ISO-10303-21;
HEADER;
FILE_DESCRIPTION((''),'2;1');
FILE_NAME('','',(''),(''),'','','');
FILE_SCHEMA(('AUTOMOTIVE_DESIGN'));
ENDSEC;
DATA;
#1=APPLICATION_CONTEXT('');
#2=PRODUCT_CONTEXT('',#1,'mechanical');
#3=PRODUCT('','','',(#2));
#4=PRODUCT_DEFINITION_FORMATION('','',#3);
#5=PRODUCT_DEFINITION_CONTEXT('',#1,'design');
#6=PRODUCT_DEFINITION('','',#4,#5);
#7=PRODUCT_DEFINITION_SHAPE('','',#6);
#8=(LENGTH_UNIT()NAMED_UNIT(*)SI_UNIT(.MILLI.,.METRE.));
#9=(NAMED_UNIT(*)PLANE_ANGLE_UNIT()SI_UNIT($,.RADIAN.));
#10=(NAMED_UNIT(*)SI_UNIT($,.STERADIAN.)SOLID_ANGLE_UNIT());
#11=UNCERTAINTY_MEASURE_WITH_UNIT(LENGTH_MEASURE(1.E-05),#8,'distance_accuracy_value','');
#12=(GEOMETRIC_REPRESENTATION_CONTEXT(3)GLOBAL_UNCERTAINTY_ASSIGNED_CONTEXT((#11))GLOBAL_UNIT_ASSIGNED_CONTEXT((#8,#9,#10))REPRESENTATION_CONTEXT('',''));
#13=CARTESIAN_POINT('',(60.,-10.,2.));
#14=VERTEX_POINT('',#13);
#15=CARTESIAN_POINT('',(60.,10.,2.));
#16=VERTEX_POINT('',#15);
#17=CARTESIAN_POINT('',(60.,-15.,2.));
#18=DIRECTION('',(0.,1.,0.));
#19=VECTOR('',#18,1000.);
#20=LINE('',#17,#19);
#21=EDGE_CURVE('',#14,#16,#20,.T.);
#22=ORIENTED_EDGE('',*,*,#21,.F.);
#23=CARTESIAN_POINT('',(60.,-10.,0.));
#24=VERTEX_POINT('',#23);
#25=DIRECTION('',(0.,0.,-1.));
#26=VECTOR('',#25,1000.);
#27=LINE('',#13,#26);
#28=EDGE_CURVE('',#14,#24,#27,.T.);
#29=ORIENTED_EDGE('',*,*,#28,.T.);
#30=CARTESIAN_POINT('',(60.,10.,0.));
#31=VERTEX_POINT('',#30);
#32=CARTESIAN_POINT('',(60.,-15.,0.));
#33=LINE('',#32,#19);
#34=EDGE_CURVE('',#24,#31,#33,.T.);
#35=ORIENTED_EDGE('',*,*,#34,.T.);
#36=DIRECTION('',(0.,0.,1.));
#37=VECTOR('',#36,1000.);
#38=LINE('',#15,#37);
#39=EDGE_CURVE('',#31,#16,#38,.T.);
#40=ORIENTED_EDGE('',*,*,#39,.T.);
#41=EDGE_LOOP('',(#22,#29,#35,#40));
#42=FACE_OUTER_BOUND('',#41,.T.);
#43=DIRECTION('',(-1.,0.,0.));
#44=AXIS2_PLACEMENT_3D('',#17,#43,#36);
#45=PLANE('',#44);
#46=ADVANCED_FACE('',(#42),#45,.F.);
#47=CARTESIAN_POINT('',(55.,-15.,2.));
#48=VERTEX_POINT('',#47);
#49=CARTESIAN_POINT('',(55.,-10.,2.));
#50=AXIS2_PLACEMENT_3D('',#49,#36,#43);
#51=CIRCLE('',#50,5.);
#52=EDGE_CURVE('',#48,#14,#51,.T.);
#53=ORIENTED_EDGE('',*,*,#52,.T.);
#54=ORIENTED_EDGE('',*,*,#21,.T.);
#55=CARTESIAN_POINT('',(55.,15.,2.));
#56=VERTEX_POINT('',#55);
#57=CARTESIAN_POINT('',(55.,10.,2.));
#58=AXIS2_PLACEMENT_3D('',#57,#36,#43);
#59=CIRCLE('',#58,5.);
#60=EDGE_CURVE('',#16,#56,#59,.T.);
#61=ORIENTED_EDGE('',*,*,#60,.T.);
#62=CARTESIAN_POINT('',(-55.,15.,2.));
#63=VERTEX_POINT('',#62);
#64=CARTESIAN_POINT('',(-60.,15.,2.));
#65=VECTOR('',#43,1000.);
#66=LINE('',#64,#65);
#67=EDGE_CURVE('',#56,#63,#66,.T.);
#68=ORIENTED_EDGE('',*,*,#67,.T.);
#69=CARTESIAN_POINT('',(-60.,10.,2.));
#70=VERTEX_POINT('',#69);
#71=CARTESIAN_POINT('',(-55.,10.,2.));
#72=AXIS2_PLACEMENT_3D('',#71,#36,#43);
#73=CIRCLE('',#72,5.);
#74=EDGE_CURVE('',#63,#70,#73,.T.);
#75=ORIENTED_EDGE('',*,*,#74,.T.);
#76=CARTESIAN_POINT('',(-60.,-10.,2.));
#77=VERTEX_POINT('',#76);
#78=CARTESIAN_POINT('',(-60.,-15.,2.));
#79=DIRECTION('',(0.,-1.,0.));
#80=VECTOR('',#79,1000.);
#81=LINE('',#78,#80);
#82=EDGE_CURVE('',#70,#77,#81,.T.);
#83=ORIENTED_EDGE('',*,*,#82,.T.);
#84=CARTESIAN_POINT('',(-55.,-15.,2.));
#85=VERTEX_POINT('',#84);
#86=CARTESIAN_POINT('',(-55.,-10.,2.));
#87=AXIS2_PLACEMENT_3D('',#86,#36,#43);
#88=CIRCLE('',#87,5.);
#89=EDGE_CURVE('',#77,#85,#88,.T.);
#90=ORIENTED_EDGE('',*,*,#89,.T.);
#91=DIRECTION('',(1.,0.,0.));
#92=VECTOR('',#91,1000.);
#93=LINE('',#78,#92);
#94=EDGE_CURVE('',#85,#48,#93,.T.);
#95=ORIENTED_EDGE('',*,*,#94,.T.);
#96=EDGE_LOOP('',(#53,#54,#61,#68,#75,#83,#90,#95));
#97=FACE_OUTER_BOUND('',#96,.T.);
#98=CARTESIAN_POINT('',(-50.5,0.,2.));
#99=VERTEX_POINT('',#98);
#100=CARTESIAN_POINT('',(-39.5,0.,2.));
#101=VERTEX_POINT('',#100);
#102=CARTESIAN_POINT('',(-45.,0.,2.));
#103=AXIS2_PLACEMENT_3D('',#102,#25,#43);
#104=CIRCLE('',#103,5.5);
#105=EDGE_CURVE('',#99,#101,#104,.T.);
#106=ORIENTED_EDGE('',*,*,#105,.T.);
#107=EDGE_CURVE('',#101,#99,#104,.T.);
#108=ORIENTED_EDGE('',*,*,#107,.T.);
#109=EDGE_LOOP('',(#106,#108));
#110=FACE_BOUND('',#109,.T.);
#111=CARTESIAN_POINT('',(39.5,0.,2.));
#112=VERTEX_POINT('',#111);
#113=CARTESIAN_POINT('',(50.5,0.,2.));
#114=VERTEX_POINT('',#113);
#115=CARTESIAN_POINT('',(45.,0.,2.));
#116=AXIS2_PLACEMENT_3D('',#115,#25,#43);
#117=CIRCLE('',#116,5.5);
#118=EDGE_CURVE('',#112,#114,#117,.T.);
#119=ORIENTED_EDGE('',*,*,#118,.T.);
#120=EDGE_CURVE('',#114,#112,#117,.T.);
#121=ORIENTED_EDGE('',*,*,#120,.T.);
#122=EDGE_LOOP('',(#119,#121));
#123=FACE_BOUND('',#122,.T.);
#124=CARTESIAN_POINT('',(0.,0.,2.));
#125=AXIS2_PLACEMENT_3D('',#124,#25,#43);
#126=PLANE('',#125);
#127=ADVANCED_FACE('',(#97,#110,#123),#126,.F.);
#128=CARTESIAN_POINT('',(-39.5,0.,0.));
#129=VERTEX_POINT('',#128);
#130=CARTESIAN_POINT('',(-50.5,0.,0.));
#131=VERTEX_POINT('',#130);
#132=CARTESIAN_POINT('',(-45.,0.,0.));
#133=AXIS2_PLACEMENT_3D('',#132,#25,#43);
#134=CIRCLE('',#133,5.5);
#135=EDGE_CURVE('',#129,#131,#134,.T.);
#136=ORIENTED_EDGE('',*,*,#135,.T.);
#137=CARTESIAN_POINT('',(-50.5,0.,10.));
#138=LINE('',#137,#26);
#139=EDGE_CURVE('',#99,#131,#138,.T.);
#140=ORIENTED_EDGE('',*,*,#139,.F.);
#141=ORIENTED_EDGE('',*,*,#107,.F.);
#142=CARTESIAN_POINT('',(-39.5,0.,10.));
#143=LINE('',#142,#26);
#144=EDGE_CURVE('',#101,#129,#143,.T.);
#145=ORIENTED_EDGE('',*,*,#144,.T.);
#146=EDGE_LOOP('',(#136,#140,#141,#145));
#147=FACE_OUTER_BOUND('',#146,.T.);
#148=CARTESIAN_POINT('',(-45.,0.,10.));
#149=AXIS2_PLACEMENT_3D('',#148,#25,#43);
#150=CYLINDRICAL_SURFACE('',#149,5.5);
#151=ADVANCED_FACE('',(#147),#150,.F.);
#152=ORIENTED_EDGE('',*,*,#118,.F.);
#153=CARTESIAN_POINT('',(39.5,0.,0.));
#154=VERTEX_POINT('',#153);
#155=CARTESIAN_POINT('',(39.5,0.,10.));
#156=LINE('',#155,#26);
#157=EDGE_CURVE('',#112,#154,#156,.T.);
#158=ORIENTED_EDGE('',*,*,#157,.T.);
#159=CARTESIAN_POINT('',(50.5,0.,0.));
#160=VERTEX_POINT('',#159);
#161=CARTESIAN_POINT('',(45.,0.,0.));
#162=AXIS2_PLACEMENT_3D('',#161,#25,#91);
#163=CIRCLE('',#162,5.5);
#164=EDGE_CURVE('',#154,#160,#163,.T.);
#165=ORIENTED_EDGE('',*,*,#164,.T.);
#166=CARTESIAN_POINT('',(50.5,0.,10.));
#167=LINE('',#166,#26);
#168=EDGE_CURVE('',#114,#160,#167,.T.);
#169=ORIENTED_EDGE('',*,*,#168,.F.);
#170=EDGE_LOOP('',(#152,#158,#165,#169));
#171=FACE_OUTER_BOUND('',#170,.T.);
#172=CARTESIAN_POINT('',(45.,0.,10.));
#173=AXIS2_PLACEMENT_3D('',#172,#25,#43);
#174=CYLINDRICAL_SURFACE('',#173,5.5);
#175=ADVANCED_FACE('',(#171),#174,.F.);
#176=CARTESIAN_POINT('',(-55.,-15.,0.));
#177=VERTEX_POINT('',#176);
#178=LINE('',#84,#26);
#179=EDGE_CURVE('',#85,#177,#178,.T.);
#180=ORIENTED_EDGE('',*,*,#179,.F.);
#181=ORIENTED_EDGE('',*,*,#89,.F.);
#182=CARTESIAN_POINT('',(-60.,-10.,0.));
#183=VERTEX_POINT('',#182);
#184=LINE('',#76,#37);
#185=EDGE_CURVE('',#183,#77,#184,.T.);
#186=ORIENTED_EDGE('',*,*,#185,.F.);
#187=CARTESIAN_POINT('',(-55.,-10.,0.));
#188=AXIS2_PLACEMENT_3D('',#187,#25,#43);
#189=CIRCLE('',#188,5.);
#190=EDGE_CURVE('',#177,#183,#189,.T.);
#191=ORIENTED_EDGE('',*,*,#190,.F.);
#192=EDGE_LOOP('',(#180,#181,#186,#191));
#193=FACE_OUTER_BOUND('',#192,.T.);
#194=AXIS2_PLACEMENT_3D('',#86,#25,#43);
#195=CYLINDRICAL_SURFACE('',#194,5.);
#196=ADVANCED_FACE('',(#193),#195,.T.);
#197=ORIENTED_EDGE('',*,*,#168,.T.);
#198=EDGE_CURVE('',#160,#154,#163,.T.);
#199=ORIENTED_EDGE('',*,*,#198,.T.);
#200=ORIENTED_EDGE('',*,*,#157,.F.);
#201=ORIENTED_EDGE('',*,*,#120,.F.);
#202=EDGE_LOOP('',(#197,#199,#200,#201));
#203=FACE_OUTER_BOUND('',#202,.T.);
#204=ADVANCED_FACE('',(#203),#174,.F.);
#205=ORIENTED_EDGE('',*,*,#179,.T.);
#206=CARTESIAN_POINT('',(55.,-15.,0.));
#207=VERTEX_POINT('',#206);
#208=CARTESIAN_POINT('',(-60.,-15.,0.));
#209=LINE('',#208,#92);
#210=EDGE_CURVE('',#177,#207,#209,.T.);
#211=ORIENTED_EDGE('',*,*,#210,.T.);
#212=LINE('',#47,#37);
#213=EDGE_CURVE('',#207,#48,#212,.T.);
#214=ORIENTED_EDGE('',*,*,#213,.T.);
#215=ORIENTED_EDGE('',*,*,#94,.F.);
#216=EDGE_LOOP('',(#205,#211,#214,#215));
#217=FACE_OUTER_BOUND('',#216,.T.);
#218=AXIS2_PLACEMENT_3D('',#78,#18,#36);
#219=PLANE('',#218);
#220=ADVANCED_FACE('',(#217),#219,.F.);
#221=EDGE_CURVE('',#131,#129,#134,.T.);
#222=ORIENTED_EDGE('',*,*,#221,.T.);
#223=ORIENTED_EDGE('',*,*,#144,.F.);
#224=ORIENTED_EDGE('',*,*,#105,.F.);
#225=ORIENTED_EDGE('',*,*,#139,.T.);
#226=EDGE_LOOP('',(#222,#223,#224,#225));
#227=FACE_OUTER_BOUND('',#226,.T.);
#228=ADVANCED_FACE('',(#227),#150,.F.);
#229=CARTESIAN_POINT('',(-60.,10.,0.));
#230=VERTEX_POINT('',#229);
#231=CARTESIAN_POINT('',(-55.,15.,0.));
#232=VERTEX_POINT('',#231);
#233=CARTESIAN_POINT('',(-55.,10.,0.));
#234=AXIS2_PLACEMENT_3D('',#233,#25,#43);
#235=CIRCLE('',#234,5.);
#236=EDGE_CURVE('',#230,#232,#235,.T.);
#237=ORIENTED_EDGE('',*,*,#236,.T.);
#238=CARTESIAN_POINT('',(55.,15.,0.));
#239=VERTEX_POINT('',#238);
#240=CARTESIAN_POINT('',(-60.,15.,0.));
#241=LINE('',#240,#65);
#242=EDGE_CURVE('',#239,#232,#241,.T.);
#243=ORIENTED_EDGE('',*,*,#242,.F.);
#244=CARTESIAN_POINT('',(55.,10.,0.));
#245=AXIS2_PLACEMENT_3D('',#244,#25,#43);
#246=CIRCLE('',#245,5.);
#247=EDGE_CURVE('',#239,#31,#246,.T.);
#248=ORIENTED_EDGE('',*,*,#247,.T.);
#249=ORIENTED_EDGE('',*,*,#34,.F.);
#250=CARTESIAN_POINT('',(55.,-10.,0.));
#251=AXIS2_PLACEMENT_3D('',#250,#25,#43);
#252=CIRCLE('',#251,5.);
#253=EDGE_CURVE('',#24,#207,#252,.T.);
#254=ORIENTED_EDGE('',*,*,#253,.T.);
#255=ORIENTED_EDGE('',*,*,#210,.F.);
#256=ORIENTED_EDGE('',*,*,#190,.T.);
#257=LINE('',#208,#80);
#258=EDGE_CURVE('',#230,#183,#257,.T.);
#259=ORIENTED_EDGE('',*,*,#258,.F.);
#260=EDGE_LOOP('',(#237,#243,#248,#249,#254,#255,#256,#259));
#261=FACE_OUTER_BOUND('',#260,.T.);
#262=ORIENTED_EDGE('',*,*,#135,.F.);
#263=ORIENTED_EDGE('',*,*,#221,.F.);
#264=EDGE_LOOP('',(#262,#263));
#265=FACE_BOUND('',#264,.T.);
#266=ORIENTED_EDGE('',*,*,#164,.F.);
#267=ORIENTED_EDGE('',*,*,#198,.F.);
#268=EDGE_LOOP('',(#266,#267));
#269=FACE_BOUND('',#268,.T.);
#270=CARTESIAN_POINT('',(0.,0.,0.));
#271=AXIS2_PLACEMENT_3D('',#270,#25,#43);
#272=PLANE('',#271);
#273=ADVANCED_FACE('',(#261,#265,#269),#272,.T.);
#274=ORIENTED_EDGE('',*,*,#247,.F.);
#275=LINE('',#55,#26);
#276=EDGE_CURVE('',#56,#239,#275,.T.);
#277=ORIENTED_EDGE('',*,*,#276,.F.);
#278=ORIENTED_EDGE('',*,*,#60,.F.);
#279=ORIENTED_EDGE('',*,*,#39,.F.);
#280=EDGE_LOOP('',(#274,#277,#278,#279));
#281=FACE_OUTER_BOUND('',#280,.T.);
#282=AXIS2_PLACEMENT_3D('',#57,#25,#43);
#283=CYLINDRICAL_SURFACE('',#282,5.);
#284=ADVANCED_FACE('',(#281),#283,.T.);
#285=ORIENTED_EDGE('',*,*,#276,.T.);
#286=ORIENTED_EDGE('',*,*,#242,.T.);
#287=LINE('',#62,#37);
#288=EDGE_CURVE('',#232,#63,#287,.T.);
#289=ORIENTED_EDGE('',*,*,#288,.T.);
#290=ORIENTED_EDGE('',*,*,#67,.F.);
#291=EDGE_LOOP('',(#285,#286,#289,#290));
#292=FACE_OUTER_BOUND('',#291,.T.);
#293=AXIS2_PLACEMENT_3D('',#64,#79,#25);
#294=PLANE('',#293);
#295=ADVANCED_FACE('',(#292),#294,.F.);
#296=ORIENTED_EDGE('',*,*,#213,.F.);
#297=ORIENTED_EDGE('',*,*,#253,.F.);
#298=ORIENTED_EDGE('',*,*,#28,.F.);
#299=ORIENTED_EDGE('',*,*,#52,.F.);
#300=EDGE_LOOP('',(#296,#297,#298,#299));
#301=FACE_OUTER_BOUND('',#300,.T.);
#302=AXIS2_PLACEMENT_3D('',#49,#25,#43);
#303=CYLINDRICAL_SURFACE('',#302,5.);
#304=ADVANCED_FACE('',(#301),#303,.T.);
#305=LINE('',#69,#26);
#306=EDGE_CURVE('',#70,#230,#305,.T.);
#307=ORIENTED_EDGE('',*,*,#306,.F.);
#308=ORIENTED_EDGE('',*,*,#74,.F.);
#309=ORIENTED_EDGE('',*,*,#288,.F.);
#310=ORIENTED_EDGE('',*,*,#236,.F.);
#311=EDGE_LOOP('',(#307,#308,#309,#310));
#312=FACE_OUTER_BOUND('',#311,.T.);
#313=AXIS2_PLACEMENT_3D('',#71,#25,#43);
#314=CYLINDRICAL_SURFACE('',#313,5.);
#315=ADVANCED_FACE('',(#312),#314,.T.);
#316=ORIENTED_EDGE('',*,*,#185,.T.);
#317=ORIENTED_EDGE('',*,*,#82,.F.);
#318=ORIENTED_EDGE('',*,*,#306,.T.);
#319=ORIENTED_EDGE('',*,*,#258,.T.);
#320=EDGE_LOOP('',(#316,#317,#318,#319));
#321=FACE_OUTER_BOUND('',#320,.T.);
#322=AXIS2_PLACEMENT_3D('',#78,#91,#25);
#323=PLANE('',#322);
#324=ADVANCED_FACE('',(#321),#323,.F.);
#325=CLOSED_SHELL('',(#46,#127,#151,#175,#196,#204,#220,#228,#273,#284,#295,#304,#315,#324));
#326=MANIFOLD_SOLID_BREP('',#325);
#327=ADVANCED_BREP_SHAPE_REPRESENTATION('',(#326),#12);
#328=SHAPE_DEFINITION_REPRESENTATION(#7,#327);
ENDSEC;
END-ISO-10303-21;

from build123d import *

# Parameters (mm, degrees)
SKETCH_1_W          = 120
SKETCH_1_H          = 30
EXTRUDE_1_DEPTH     = 2
SKETCH_2_R          = 5.5
CUT_EXTRUDE_1_DEPTH = 10
FILLET_1_R          = 5


with BuildPart() as part:
    # 草图1 → 凸台-拉伸1 (new body)
    with BuildSketch(Plane.XY):
        Rectangle(SKETCH_1_W, SKETCH_1_H)
    extrude(amount=EXTRUDE_1_DEPTH)

    # 草图2 → 切除-拉伸1 (cut)
    with BuildSketch(Plane(origin=(0, 0, 0), x_dir=(-1, 0, 0), z_dir=(0, 0, -1))):
        with Locations((45, 0)):
            Circle(SKETCH_2_R)
        with Locations((-45, 0)):
            Circle(SKETCH_2_R)
    extrude(amount=-CUT_EXTRUDE_1_DEPTH, mode=Mode.SUBTRACT)

    # 圆角1
    fillet_1_edges = [part.edges().sort_by_distance(p)[0] for p in [
        (60, -15, 1),
        (-60, -15, 1),
        (-60, 15, 1),
        (60, 15, 1),
    ]]
    fillet(fillet_1_edges, radius=FILLET_1_R)


solid = part.part
